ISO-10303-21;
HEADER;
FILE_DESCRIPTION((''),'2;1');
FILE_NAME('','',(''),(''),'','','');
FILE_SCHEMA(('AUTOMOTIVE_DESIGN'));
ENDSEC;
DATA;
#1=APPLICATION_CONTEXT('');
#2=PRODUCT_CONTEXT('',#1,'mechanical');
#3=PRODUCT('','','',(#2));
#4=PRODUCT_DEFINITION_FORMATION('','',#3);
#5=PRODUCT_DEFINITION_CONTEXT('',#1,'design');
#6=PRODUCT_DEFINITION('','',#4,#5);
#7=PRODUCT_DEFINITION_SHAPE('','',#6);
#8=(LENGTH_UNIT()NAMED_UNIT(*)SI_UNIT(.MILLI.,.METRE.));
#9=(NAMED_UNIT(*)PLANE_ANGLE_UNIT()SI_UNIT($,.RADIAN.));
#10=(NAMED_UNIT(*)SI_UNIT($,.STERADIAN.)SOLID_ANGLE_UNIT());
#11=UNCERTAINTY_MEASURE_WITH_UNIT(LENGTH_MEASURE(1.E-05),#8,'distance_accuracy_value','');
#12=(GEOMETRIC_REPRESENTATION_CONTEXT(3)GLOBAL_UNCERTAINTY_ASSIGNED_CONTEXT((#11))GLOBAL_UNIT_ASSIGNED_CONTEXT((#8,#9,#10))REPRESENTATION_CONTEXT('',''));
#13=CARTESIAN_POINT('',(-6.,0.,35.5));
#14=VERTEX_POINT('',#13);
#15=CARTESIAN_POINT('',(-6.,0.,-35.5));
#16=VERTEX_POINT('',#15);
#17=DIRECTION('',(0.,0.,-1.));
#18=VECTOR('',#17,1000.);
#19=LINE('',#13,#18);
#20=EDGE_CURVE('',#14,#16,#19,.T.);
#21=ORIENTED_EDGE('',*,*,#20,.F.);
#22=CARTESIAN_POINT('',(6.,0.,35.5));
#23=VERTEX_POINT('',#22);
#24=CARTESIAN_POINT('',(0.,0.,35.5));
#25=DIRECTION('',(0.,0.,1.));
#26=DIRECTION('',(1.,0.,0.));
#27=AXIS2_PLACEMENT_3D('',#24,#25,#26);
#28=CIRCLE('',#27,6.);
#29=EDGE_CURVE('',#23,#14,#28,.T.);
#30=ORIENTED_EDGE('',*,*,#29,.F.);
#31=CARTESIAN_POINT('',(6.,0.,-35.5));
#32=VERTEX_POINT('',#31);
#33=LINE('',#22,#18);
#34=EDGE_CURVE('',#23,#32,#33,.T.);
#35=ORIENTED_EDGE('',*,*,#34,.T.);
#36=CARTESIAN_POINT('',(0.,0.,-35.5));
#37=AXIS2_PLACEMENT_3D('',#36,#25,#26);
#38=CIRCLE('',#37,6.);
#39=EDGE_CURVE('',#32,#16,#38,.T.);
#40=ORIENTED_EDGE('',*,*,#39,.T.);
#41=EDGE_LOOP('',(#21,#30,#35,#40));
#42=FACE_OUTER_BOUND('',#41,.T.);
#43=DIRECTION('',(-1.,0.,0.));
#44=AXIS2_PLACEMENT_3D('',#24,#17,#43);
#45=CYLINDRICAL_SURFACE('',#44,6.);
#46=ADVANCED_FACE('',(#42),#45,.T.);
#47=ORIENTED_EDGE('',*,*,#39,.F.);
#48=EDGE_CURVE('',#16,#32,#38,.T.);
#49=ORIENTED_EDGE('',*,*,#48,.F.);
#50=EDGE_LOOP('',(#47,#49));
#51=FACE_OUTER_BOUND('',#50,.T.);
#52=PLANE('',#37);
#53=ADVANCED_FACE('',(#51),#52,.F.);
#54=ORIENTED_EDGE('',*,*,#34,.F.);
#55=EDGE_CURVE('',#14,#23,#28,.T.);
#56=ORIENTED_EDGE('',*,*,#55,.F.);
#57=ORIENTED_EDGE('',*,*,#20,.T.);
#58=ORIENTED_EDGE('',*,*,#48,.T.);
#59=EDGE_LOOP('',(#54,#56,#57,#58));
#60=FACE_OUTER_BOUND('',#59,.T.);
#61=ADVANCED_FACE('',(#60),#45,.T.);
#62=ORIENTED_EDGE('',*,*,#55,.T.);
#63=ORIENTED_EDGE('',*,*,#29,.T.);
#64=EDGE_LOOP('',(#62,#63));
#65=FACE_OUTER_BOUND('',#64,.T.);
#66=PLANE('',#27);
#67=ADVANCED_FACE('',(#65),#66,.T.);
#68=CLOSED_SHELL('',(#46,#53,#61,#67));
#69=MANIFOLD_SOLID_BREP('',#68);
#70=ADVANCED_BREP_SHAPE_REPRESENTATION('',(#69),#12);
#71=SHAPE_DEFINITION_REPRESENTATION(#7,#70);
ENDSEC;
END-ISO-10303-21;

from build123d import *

# Parameters (mm, degrees)
SKETCH_1_R      = 6
EXTRUDE_1_DEPTH = 35.5


with BuildPart() as part:
    # 草图1 → 凸台-拉伸1 (new, symmetric)
    with BuildSketch(Plane.XY):
        Circle(SKETCH_1_R)
    extrude(amount=EXTRUDE_1_DEPTH, both=True)


solid = part.part
